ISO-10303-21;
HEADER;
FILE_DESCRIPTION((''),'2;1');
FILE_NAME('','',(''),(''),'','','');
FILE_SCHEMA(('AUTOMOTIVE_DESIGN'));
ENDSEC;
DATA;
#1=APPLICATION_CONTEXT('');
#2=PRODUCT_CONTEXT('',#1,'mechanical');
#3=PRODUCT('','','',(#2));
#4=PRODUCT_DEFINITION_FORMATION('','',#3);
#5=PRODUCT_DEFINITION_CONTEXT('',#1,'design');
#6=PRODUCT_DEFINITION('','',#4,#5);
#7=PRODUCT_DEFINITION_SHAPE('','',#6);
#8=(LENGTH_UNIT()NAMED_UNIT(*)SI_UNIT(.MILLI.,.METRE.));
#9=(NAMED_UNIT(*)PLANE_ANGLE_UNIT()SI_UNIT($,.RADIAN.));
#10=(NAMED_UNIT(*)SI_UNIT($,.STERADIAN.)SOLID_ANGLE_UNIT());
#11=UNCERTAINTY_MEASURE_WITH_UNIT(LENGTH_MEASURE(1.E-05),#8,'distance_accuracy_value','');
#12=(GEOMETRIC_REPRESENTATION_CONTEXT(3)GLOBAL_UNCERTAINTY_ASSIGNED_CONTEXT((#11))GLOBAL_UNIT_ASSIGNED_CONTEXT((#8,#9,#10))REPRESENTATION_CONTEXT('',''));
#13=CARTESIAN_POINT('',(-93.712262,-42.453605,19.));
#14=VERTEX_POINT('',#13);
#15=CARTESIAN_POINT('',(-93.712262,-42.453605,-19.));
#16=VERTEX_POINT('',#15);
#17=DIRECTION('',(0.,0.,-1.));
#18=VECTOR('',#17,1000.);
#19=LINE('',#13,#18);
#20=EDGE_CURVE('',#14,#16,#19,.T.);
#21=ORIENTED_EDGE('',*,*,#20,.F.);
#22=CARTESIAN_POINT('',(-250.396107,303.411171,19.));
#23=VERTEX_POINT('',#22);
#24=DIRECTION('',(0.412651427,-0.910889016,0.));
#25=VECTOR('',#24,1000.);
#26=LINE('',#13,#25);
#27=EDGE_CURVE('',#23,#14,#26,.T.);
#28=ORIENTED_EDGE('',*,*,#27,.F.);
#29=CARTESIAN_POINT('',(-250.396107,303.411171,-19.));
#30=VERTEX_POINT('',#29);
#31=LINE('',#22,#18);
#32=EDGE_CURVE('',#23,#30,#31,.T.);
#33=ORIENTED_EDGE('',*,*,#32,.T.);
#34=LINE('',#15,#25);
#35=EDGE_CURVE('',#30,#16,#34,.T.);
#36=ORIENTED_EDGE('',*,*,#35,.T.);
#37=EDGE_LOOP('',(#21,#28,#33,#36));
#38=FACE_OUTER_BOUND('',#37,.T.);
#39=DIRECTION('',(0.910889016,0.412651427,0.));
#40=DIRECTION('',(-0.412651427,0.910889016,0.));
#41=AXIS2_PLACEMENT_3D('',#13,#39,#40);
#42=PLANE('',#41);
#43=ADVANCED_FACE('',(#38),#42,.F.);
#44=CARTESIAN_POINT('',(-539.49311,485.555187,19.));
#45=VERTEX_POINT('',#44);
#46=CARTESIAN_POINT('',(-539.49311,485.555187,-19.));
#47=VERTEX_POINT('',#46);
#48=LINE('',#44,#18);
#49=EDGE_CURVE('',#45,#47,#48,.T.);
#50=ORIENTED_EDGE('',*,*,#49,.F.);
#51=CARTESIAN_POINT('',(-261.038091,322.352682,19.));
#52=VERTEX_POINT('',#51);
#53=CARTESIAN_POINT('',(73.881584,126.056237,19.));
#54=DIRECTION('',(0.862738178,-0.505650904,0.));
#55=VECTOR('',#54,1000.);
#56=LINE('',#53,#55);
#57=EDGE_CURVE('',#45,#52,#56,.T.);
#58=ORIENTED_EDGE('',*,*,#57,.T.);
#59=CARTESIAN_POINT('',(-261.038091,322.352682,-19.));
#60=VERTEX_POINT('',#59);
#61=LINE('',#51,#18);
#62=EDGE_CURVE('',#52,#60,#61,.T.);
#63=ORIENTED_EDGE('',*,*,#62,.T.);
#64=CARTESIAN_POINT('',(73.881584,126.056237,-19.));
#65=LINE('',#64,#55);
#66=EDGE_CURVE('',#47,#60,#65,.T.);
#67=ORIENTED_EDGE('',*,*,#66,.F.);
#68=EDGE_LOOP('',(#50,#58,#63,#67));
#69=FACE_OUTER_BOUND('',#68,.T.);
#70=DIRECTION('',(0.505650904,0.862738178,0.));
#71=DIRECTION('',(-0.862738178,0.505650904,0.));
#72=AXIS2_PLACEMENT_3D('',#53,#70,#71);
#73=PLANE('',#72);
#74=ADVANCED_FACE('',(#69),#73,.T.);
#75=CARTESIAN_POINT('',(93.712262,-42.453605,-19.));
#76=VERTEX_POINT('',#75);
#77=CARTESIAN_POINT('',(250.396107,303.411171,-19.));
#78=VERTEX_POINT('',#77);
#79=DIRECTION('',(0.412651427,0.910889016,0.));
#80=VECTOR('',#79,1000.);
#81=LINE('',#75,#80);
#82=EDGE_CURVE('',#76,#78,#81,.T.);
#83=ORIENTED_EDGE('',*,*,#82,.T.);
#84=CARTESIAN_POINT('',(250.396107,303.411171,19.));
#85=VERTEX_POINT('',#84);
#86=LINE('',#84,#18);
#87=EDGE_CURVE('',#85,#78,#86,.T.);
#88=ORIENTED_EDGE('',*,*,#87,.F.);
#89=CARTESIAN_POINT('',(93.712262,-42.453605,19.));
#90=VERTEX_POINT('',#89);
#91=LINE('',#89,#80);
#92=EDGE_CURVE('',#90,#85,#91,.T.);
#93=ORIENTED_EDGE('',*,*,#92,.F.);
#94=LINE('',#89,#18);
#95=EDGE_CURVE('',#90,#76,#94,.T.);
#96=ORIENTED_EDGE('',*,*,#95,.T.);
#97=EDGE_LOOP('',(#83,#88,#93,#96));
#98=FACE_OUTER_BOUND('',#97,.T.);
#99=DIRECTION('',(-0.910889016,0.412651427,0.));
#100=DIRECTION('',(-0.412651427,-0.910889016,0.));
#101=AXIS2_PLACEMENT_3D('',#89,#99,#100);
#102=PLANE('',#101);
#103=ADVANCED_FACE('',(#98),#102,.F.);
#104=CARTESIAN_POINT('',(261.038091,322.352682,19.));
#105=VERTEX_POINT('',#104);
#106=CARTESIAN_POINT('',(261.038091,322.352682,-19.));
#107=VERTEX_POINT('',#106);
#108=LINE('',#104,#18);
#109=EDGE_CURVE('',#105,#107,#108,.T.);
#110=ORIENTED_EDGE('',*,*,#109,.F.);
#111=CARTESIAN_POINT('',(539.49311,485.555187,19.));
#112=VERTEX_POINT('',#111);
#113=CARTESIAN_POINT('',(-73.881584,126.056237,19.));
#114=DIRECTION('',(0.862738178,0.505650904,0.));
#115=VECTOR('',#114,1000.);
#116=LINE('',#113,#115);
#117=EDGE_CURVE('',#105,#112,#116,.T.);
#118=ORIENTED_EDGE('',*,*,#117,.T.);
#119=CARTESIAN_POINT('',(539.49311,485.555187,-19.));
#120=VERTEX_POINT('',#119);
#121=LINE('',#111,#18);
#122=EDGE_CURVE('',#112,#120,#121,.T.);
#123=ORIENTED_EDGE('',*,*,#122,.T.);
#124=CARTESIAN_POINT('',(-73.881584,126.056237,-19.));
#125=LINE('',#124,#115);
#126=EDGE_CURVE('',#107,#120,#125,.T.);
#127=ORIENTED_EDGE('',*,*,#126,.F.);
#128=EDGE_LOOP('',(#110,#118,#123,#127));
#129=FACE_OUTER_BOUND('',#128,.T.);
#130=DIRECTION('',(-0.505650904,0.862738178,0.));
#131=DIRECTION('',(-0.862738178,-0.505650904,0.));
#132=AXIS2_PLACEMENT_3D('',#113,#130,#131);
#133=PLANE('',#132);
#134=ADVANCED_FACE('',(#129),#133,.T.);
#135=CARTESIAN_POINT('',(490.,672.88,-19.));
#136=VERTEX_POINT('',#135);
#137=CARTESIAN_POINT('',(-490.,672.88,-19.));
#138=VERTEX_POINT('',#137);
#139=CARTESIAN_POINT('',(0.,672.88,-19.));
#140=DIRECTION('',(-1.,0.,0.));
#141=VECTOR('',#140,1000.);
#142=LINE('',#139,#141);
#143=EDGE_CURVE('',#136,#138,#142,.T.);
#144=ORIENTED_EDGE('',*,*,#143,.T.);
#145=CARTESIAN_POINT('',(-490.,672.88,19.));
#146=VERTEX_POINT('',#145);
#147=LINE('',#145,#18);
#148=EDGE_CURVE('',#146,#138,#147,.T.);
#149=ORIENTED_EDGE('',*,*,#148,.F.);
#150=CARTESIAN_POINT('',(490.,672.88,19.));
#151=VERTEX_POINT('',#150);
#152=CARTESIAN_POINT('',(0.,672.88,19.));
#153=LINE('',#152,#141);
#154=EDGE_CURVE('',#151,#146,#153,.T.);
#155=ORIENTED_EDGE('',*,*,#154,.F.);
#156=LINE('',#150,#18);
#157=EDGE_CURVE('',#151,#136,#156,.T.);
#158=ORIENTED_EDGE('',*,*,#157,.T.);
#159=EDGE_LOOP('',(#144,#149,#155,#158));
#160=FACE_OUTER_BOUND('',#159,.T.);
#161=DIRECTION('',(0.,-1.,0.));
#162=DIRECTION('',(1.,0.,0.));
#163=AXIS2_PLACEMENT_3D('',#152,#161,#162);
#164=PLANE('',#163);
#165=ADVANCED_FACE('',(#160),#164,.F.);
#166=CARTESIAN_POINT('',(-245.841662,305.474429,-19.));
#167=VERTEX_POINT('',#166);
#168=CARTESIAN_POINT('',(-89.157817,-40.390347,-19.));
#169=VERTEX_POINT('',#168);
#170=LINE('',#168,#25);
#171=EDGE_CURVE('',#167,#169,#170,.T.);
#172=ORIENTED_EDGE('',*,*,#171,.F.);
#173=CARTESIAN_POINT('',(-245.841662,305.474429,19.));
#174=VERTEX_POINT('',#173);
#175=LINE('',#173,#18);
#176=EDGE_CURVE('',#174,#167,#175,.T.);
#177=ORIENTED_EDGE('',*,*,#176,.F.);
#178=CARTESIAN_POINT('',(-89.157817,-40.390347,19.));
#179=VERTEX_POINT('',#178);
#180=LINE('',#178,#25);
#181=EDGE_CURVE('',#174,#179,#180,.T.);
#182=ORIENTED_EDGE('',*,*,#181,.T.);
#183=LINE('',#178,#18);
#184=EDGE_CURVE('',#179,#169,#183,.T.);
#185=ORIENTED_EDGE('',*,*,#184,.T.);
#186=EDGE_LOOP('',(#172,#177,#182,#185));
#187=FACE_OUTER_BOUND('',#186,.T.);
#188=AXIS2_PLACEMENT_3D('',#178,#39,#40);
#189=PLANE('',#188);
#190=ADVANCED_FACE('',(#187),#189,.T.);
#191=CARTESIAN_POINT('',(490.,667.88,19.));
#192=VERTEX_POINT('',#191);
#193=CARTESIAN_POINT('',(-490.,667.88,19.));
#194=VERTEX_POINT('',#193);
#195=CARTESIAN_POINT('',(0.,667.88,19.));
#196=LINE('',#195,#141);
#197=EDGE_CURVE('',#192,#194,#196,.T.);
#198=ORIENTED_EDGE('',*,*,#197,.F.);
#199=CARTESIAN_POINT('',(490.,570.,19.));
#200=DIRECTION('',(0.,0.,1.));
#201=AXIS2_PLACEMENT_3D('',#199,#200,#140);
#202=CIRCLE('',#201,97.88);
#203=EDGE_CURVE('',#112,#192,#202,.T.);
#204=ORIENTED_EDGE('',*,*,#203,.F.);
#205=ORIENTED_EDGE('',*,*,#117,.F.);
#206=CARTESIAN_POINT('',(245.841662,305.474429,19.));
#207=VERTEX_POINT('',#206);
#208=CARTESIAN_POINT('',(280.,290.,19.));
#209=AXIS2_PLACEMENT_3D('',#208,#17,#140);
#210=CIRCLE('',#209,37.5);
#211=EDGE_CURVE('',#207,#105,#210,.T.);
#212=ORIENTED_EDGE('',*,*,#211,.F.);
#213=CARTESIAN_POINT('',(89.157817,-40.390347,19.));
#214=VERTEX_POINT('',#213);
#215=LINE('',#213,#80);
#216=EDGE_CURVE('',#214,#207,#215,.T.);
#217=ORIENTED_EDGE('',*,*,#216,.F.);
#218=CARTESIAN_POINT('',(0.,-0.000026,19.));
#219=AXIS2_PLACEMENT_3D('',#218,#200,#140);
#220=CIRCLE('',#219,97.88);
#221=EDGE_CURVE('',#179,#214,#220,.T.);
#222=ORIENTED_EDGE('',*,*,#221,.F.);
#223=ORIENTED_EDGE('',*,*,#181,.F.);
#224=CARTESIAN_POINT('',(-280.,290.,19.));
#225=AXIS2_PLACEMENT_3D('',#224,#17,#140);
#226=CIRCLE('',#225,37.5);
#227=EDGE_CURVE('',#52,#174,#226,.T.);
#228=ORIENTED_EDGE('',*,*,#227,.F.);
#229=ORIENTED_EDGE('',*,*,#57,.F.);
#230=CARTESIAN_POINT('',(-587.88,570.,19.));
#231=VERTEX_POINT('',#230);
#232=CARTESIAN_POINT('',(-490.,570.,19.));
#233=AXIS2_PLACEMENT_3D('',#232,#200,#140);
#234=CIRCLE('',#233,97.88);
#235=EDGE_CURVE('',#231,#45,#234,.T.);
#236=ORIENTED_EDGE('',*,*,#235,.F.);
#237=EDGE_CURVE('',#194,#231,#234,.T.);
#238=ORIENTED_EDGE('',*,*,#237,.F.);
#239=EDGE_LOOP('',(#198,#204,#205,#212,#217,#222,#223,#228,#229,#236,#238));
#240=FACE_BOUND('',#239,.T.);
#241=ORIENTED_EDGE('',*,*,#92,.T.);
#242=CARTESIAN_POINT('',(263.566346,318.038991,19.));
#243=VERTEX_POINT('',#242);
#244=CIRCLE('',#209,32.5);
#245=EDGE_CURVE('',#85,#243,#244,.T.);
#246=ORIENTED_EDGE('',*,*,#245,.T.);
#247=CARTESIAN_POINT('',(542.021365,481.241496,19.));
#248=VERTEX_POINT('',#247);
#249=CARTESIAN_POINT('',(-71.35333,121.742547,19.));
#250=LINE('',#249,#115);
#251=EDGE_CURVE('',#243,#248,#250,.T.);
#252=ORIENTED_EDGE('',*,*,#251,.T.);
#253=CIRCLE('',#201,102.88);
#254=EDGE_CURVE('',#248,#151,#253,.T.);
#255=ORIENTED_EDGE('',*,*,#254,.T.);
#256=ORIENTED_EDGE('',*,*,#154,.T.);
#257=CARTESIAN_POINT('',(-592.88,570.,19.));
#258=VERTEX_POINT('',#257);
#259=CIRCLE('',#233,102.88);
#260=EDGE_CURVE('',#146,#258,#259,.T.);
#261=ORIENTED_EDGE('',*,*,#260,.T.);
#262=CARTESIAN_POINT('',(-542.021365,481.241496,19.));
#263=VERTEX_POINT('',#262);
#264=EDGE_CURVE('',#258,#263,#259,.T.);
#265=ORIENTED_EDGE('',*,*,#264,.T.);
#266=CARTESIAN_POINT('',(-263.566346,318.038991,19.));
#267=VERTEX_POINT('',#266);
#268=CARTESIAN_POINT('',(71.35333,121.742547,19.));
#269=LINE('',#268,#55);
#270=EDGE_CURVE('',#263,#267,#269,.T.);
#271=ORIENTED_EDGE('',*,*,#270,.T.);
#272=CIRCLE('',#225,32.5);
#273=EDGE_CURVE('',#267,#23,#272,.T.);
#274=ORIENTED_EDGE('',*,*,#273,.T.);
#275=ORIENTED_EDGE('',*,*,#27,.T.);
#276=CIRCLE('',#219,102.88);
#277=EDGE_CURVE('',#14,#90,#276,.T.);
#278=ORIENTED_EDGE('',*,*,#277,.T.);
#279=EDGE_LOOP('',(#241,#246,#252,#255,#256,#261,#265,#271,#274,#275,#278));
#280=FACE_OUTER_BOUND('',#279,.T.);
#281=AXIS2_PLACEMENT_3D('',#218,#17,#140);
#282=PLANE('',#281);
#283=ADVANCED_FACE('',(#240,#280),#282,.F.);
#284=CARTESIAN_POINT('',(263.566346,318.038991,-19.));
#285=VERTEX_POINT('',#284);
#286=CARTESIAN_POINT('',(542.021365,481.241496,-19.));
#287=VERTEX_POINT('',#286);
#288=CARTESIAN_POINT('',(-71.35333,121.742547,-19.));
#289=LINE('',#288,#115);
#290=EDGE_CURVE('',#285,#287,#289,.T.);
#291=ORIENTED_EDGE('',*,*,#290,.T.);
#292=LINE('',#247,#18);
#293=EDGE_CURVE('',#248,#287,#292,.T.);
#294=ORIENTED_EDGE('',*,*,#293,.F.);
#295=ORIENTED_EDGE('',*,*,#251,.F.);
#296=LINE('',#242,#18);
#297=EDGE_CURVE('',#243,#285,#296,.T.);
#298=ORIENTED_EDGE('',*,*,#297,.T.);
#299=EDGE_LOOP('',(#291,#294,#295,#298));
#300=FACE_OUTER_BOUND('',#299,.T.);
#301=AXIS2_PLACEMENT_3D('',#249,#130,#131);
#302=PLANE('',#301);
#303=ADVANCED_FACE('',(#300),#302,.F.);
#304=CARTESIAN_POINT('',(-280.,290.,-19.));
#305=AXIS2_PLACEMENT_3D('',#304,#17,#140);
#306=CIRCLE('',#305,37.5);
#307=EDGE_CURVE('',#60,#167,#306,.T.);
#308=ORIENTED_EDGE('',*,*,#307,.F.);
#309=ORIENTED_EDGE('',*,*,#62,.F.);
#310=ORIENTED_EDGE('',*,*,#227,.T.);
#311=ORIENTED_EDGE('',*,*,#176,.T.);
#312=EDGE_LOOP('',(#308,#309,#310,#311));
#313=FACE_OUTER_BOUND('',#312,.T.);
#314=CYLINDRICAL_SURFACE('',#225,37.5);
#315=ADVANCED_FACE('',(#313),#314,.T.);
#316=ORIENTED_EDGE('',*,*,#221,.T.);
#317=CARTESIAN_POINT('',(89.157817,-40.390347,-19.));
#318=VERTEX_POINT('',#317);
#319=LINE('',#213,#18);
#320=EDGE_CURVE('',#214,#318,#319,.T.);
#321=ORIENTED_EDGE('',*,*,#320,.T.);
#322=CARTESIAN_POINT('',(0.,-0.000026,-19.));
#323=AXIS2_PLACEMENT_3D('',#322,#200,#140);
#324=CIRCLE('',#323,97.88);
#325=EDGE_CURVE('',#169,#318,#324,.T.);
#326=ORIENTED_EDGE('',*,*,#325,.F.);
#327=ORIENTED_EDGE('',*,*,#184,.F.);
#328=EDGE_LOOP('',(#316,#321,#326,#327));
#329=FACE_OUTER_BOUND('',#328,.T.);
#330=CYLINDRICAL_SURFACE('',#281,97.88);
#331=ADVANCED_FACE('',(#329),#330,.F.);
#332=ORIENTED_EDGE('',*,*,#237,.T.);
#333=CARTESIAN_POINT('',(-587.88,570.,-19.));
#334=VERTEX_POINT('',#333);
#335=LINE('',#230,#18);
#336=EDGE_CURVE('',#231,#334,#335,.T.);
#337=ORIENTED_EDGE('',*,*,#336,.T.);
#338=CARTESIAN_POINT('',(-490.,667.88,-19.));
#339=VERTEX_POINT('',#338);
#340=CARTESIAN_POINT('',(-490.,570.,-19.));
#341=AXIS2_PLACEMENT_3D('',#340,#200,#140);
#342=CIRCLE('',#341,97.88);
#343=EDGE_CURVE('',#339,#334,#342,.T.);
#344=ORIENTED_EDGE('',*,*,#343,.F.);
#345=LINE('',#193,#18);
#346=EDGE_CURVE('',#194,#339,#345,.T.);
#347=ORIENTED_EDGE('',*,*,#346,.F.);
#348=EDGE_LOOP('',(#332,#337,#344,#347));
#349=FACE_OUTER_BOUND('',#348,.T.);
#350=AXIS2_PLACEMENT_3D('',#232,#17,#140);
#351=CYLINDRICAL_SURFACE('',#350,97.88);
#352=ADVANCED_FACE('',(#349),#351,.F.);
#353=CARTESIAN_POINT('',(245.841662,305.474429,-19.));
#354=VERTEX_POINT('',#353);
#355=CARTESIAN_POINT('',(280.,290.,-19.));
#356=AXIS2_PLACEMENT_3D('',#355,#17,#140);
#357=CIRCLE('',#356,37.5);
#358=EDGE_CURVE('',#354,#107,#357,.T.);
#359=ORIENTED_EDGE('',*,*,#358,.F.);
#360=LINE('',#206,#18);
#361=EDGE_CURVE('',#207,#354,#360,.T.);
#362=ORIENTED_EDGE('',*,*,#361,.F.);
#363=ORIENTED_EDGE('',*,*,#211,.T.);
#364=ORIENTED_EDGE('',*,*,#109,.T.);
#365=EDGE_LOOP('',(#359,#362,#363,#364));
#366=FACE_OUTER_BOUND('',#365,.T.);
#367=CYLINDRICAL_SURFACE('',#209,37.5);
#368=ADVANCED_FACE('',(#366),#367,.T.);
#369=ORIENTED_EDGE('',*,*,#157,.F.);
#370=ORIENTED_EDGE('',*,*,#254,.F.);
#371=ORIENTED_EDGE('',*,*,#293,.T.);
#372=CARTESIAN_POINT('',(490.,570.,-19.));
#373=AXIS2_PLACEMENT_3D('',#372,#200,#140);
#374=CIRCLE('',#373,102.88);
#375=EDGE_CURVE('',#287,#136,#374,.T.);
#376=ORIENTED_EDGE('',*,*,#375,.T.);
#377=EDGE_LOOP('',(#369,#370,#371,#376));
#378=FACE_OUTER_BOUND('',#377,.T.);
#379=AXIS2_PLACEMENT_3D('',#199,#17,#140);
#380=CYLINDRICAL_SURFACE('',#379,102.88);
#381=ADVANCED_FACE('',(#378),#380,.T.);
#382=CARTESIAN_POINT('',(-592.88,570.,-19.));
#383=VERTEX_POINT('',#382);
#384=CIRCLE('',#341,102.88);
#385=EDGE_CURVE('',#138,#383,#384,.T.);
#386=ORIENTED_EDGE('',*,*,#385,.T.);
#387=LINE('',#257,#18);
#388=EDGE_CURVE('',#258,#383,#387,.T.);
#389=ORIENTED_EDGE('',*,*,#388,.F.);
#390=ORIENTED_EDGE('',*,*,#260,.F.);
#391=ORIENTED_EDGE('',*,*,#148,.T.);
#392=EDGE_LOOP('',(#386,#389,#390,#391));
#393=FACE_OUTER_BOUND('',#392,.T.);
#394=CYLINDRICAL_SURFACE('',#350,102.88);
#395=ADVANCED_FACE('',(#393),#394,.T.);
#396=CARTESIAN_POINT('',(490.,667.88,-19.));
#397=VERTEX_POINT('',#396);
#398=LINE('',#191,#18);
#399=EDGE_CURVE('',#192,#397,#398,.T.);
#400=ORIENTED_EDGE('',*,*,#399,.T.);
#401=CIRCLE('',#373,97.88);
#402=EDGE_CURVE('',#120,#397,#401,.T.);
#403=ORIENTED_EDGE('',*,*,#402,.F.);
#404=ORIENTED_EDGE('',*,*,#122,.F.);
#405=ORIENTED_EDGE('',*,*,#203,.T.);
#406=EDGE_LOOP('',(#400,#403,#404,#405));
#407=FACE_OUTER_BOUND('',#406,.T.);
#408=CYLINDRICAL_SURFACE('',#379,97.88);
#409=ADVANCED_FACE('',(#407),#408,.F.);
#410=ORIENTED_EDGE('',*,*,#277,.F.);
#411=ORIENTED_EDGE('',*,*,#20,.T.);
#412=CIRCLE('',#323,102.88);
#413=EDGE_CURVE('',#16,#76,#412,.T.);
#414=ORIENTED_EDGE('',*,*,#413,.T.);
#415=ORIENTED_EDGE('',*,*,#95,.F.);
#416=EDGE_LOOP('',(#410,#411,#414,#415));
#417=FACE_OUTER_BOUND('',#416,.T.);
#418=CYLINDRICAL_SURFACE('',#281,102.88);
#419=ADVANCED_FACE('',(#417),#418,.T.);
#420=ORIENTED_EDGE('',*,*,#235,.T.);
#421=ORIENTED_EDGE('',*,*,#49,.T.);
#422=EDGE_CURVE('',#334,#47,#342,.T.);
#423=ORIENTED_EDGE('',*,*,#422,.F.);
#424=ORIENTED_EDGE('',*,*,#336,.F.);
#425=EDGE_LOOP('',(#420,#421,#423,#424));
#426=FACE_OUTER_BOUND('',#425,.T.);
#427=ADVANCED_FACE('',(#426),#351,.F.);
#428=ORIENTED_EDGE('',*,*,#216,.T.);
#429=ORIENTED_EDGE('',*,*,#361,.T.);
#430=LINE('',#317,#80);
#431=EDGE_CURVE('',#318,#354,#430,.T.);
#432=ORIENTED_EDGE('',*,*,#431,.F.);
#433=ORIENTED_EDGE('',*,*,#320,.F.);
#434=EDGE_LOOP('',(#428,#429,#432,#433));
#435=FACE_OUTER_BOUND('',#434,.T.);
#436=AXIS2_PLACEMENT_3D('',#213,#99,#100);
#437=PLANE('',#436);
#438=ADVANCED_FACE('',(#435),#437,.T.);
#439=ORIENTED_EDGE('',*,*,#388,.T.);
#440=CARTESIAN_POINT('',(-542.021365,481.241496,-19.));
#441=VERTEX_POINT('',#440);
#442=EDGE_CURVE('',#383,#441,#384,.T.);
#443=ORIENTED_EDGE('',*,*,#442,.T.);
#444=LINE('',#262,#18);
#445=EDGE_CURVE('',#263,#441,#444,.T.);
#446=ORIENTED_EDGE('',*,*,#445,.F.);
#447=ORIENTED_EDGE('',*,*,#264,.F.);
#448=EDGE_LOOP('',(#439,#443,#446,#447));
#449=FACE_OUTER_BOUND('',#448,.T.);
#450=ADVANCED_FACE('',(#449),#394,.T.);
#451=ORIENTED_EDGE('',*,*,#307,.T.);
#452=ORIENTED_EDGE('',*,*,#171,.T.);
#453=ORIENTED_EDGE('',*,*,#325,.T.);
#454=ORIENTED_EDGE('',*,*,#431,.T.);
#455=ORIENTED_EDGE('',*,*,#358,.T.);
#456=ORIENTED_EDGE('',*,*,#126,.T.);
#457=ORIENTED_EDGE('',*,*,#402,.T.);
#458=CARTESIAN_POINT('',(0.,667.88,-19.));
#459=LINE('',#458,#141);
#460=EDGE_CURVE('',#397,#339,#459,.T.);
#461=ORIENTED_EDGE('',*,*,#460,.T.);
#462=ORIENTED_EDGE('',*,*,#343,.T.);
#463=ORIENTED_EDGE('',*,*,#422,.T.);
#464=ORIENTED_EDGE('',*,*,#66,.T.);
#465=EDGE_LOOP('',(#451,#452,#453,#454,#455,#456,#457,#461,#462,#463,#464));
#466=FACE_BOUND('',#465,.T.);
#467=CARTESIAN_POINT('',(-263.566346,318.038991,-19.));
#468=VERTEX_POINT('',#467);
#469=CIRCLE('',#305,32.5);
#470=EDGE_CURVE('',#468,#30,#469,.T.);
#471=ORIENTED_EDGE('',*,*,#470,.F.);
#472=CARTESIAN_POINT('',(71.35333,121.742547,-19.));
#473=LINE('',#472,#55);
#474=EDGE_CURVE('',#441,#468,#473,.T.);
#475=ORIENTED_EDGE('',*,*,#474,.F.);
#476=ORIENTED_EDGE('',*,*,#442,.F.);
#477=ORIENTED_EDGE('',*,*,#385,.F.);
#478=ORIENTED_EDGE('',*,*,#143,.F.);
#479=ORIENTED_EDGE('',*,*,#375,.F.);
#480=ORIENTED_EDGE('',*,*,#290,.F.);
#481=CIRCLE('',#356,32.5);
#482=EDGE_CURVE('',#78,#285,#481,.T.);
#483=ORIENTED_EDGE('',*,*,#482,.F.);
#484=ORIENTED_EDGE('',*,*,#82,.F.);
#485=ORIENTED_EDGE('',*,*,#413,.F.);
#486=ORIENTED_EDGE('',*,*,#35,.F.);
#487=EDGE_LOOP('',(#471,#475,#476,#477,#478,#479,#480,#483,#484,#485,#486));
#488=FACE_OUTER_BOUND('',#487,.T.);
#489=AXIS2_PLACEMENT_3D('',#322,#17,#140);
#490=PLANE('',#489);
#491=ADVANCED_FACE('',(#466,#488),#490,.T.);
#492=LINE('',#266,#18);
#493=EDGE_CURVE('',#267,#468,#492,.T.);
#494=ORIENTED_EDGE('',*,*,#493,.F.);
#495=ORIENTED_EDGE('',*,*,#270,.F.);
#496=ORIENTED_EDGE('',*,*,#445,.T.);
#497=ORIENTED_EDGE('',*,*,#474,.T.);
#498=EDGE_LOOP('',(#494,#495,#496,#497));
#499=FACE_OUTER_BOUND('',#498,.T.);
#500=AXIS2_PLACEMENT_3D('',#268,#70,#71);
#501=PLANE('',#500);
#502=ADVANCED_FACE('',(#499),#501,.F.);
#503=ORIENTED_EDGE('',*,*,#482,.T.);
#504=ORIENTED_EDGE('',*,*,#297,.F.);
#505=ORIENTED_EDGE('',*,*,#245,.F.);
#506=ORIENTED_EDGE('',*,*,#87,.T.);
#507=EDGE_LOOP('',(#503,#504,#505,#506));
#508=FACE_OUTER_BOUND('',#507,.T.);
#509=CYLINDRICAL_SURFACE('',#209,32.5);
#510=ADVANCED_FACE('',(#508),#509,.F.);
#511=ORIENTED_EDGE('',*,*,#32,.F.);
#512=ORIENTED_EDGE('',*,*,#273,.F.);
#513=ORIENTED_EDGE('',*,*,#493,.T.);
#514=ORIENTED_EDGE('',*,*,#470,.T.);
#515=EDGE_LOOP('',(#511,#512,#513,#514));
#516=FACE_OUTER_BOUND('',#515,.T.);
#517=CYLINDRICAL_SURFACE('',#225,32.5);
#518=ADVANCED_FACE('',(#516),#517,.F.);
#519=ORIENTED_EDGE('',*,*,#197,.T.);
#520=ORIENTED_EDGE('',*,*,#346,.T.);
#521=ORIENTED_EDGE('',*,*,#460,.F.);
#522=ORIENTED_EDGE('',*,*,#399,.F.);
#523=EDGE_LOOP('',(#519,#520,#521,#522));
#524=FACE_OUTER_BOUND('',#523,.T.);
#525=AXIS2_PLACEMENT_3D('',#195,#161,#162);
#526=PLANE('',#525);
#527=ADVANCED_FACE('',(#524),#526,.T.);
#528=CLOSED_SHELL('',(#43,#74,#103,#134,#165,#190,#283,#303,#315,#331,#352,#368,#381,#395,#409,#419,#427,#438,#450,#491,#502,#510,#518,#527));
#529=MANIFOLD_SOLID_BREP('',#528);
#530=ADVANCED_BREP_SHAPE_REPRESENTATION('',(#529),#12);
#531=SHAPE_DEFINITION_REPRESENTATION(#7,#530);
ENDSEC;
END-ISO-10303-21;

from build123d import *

# Parameters (mm, degrees)
EXTRUDE_1_DEPTH = 19


with BuildPart() as part:
    # 草图2 → 拉伸-薄壁1 (new, symmetric)
    with BuildSketch(Plane.XY):
        with BuildLine():
            Line((250.396106976, 303.41117138), (93.71226198, -42.453604657))
            ThreePointArc((93.71226198, -42.453604657), (0, -102.880025838), (-93.71226198, -42.453604657))
            Line((-93.71226198, -42.453604657), (-250.396106976, 303.41117138))
            ThreePointArc((-250.396106976, 303.41117138), (-255.847210975, 311.746098094), (-263.566345627, 318.03899078))
            Line((-263.566345627, 318.03899078), (-542.021364981, 481.241496264))
            ThreePointArc((-542.021364981, 481.241496264), (-589.286880464, 596.951990053), (-490, 672.88))
            Line((-490, 672.88), (490, 672.88))
            ThreePointArc((490, 672.88), (589.286880464, 596.951990053), (542.021364981, 481.241496264))
            Line((542.021364981, 481.241496264), (263.566345627, 318.03899078))
            ThreePointArc((263.566345627, 318.03899078), (255.847210975, 311.746098094), (250.396106976, 303.41117138))
        make_face()
        with BuildLine():
            Line((245.841661895, 305.474428516), (89.1578169, -40.390347521))
            ThreePointArc((89.1578169, -40.390347521), (0, -97.880025838), (-89.1578169, -40.390347521))
            Line((-89.1578169, -40.390347521), (-245.841661895, 305.474428516))
            ThreePointArc((-245.841661895, 305.474428516), (-252.131397279, 315.091651647), (-261.038091108, 322.352681669))
            Line((-261.038091108, 322.352681669), (-539.493110463, 485.555187153))
            ThreePointArc((-539.493110463, 485.555187153), (-584.461507191, 595.642114953), (-490, 667.88))
            Line((-490, 667.88), (490, 667.88))
            ThreePointArc((490, 667.88), (584.461507191, 595.642114953), (539.493110463, 485.555187153))
            Line((539.493110463, 485.555187153), (261.038091108, 322.352681669))
            ThreePointArc((261.038091108, 322.352681669), (252.131397279, 315.091651647), (245.841661895, 305.474428516))
        make_face(mode=Mode.SUBTRACT)
    extrude(amount=EXTRUDE_1_DEPTH, both=True)


solid = part.part
